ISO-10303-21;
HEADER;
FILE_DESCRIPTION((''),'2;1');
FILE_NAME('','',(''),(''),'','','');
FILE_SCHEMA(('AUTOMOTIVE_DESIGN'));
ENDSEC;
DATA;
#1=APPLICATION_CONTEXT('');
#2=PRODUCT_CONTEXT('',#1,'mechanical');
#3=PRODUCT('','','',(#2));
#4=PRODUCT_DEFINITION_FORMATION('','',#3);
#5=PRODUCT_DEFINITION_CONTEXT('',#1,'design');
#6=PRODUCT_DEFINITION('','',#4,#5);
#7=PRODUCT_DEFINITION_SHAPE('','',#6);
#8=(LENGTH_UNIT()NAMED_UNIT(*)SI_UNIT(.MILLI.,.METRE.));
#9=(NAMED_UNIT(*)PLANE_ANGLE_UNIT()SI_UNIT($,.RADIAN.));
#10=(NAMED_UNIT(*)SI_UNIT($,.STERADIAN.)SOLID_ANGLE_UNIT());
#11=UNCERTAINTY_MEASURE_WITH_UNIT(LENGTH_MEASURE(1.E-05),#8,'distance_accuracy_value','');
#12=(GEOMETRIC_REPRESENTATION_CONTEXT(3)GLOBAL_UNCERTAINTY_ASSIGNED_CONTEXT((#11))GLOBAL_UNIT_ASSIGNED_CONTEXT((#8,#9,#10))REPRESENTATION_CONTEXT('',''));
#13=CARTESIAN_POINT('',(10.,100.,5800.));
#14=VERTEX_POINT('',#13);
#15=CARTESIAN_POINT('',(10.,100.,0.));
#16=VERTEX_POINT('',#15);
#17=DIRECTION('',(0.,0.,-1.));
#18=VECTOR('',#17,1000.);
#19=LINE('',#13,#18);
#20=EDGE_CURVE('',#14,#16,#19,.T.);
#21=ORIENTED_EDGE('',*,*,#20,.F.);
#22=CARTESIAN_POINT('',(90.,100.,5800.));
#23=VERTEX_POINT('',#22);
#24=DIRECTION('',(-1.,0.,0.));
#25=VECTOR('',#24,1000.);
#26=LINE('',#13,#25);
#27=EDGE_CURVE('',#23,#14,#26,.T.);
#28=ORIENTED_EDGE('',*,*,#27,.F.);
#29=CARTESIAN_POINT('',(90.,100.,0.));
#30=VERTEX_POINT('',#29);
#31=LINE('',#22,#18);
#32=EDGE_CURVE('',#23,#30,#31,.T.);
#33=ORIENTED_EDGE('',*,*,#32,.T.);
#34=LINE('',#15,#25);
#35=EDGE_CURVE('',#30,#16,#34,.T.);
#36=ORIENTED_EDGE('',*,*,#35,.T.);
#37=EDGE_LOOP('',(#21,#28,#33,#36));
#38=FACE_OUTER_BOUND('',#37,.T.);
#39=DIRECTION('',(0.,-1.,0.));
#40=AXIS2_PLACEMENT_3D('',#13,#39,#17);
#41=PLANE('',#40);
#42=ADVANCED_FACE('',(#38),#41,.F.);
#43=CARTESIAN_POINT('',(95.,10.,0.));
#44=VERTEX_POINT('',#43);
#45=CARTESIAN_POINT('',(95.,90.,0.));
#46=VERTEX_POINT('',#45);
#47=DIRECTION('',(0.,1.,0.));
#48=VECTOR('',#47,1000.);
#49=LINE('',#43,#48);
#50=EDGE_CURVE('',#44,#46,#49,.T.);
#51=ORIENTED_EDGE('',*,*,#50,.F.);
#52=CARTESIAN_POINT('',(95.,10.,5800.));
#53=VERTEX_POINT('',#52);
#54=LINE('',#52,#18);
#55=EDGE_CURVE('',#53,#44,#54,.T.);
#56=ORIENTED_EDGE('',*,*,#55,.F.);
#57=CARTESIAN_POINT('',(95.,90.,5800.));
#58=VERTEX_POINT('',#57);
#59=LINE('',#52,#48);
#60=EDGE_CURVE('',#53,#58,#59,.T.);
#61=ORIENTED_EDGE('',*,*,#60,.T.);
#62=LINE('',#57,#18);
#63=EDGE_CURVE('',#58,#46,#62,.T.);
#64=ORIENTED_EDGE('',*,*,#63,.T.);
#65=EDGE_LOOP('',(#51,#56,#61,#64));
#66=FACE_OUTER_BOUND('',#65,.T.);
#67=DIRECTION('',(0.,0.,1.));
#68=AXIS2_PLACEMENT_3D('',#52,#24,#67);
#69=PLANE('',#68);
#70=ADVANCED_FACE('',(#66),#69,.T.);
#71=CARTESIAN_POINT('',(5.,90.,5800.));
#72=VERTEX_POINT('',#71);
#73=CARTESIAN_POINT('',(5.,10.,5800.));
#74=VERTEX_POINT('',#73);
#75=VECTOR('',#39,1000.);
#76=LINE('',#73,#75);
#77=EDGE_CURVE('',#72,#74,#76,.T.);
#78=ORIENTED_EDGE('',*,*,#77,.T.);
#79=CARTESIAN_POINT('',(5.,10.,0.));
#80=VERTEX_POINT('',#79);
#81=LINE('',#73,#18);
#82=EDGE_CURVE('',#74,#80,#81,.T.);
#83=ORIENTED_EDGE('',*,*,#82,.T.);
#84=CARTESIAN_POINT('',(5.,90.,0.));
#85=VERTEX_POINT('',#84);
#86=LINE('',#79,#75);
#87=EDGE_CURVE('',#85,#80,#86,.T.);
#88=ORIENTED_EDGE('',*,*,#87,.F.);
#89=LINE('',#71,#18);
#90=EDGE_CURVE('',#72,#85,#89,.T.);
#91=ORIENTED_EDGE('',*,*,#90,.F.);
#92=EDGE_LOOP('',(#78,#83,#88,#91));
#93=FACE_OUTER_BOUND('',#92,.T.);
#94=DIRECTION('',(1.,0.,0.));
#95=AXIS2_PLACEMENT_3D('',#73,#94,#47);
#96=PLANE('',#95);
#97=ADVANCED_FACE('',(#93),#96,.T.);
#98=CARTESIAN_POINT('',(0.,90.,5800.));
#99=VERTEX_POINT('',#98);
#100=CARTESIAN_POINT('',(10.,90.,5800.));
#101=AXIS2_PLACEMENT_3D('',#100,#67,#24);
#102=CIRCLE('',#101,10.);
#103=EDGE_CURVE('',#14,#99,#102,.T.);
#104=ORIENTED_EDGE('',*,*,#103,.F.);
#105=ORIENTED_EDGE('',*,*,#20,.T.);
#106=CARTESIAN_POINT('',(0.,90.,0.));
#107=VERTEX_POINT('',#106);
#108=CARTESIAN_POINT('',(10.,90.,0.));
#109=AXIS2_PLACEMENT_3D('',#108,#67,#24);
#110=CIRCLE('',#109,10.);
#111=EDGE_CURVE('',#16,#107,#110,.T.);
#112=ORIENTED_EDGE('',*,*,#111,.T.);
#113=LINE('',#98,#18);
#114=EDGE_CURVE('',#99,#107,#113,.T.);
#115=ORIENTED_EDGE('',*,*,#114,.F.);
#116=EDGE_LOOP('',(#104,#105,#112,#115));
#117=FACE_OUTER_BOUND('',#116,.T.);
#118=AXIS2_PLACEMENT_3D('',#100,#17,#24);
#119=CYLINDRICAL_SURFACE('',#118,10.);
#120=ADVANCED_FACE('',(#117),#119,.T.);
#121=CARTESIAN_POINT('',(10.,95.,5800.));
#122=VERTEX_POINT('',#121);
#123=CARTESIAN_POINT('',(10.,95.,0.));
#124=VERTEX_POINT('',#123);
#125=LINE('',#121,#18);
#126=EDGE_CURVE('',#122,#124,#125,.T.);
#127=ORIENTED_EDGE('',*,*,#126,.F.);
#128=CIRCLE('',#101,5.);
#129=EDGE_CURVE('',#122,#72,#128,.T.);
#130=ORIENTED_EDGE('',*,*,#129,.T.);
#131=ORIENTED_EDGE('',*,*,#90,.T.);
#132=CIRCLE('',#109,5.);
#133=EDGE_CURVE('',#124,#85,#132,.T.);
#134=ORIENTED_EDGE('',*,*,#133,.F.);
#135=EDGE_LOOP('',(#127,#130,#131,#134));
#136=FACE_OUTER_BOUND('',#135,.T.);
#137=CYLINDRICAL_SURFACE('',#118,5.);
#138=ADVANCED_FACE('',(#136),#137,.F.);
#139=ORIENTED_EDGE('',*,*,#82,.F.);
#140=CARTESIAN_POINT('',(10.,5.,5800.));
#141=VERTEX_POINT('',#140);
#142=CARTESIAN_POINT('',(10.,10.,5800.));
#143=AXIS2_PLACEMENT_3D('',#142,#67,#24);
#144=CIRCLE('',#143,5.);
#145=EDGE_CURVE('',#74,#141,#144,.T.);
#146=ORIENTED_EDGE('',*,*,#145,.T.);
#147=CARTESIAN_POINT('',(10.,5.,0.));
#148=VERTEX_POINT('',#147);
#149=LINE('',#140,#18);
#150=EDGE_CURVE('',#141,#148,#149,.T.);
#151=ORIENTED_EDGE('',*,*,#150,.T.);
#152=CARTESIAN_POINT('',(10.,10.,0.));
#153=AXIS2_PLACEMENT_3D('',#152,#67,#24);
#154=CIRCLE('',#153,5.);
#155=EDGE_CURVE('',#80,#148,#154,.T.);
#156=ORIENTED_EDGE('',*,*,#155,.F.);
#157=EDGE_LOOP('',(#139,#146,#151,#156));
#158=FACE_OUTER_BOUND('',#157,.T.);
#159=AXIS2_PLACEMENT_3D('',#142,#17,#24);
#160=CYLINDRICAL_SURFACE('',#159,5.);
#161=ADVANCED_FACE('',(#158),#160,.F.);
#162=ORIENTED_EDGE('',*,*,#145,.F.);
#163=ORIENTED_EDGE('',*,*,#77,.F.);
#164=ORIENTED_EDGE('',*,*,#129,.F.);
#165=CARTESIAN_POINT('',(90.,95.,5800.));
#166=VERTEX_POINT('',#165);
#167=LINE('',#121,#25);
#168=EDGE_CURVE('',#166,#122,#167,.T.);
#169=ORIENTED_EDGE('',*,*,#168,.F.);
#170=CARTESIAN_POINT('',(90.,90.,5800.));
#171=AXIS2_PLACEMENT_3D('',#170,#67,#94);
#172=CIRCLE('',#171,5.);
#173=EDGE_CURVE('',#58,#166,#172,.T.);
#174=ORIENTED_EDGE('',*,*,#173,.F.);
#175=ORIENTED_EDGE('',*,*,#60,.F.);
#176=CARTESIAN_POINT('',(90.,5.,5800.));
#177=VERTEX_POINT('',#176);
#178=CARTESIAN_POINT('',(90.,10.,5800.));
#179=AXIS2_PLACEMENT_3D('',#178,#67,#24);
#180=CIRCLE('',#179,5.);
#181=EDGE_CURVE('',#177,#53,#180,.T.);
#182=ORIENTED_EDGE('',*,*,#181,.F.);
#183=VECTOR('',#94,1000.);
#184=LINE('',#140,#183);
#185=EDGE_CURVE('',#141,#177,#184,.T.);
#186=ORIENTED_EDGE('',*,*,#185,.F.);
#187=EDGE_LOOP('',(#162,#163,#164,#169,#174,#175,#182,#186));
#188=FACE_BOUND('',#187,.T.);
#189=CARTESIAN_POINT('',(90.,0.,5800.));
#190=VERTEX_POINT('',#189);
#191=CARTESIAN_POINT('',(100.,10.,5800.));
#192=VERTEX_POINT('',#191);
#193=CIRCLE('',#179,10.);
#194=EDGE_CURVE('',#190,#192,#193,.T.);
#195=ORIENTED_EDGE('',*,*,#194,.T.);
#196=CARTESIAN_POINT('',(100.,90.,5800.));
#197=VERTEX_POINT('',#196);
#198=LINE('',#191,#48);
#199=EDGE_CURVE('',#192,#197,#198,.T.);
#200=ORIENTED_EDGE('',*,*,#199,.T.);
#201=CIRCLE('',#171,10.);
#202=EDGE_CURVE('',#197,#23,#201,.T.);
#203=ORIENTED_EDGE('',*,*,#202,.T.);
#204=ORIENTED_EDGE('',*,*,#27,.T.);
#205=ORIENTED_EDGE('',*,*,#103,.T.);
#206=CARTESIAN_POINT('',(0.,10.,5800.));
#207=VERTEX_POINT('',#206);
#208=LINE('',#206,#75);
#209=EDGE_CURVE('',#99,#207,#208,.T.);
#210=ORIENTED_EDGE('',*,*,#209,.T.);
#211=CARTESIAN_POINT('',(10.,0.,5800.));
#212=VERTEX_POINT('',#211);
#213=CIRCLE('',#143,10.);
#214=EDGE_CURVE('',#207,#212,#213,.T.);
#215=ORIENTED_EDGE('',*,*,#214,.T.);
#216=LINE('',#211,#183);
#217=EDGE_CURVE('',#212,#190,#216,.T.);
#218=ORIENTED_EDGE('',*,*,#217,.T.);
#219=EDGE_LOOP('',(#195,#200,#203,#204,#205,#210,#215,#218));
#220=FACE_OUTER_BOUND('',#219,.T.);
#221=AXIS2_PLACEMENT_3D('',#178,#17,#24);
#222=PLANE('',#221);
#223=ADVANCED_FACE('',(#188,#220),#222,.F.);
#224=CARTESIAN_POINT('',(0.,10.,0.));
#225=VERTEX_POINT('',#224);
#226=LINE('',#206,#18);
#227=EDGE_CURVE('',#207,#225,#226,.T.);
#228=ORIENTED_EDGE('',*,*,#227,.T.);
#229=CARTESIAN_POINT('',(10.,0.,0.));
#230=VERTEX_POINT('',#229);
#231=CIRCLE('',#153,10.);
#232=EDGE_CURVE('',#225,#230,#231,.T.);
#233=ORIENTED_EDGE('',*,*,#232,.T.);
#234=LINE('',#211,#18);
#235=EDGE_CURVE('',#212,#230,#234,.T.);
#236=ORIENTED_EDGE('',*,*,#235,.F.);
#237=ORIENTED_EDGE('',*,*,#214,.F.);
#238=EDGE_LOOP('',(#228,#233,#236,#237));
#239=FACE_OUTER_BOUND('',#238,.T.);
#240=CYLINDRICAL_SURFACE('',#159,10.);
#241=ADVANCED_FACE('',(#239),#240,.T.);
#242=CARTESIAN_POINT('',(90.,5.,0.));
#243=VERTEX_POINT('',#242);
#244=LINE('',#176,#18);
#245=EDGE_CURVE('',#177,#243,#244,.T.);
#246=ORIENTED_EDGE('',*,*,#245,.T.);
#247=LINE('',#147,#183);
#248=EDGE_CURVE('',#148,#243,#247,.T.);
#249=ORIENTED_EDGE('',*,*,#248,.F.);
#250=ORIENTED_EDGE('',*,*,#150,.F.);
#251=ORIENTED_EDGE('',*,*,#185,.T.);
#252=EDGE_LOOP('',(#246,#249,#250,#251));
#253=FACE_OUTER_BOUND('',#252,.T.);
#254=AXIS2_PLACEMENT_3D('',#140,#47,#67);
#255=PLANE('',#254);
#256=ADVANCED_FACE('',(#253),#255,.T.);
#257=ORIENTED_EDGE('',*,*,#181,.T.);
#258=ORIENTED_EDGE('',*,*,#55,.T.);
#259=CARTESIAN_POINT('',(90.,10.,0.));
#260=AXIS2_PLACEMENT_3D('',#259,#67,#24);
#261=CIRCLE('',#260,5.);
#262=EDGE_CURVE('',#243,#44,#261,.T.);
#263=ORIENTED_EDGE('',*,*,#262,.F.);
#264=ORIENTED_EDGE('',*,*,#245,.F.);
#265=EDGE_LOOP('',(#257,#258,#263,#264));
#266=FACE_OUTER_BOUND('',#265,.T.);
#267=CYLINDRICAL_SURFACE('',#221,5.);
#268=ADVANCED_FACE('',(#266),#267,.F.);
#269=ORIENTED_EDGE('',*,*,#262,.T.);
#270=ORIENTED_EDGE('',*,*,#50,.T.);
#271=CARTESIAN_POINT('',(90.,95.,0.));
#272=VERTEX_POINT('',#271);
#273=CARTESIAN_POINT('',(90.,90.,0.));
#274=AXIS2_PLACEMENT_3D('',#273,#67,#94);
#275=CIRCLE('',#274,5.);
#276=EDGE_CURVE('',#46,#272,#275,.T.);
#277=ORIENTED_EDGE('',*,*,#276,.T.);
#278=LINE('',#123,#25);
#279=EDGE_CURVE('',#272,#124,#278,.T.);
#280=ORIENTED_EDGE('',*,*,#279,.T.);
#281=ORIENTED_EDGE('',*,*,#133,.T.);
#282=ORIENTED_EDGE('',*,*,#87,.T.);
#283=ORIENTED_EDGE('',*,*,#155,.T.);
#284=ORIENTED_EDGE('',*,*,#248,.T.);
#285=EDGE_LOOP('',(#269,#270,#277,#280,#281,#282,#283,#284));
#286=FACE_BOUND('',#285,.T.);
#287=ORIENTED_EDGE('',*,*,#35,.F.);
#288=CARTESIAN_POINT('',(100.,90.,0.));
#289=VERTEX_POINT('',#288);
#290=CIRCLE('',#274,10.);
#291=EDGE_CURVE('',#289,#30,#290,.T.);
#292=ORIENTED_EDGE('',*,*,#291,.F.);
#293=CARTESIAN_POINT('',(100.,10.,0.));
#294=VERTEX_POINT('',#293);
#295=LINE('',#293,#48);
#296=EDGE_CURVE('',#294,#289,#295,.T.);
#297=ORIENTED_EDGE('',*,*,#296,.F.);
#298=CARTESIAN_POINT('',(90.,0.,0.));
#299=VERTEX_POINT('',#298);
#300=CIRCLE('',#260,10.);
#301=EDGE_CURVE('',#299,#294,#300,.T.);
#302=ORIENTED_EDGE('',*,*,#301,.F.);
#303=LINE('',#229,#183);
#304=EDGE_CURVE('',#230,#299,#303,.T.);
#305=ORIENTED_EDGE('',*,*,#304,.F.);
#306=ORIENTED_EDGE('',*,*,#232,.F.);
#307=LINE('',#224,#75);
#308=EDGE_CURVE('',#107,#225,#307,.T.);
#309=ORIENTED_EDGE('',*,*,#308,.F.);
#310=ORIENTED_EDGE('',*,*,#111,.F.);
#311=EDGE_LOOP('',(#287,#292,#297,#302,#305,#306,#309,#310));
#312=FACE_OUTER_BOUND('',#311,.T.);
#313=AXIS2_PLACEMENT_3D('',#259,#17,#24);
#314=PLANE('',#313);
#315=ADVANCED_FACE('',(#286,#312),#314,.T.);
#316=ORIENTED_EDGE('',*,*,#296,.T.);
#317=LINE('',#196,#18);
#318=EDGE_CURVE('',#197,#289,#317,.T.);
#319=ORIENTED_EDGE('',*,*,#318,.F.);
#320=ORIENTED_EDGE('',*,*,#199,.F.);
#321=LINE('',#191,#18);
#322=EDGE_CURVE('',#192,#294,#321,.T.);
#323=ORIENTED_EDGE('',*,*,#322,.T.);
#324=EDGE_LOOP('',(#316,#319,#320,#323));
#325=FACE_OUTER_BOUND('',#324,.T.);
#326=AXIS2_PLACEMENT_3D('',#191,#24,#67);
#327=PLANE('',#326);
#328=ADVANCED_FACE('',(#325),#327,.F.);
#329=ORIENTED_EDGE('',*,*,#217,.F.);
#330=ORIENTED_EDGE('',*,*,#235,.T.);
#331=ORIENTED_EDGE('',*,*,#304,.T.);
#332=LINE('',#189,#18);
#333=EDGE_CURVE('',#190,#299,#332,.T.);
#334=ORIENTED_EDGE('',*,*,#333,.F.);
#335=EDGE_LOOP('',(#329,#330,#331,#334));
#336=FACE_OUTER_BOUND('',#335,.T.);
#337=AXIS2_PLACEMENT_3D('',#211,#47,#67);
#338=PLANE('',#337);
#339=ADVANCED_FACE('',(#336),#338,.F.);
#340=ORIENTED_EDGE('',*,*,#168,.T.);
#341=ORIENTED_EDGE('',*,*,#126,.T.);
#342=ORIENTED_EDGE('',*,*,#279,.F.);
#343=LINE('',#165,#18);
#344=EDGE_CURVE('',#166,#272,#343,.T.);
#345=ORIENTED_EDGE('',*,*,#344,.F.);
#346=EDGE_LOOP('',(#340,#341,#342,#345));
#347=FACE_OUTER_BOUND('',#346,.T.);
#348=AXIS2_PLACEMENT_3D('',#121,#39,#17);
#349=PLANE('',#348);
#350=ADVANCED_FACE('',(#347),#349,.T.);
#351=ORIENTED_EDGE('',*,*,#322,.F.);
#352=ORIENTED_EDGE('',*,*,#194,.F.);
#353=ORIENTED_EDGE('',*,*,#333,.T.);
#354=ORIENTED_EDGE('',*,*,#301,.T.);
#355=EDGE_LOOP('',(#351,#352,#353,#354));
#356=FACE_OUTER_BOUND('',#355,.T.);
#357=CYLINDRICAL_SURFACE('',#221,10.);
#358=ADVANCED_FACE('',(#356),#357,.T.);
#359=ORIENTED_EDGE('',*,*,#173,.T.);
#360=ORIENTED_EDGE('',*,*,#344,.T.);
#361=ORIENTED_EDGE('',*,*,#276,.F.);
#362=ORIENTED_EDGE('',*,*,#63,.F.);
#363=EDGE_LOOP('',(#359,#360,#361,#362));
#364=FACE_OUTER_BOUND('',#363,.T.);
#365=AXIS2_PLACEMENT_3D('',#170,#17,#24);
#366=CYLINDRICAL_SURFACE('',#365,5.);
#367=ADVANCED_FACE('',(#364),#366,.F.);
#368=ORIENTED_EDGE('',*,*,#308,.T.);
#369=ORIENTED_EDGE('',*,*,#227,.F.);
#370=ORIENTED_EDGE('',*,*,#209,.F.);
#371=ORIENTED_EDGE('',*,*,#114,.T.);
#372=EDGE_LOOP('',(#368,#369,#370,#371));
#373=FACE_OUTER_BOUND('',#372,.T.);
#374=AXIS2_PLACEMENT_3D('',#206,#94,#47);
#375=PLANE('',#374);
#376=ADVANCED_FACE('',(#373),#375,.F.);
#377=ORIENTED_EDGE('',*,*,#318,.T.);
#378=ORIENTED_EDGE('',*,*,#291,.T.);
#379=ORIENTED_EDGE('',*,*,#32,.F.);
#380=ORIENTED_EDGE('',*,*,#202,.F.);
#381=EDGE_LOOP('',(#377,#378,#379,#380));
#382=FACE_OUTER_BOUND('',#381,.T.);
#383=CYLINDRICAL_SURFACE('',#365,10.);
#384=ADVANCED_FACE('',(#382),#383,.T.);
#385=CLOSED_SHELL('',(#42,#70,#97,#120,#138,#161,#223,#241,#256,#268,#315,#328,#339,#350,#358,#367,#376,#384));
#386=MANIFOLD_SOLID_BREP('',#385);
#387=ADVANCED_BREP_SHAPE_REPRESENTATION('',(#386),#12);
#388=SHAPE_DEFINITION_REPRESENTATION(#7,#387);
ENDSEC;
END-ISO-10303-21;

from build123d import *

# Parameters (mm, degrees)
BOSS_EXTRUDE1_DEPTH = 5800


with BuildPart() as part:
    # Sketch1 → Boss-Extrude1 (new body)
    with BuildSketch(Plane.XY):
        with BuildLine():
            Line((10, 0), (90, 0))
            ThreePointArc((90, 0), (97.071067812, 2.928932188), (100, 10))
            Line((100, 10), (100, 90))
            ThreePointArc((100, 90), (97.071067812, 97.071067812), (90, 100))
            Line((90, 100), (10, 100))
            ThreePointArc((10, 100), (2.928932188, 97.071067812), (0, 90))
            Line((0, 90), (0, 10))
            ThreePointArc((0, 10), (2.928932188, 2.928932188), (10, 0))
        make_face()
        with BuildLine():
            Line((10, 95), (90, 95))
            ThreePointArc((90, 95), (93.535533906, 93.535533906), (95, 90))
            Line((95, 90), (95, 10))
            ThreePointArc((95, 10), (93.535533906, 6.464466094), (90, 5))
            Line((90, 5), (10, 5))
            ThreePointArc((10, 5), (6.464466094, 6.464466094), (5, 10))
            Line((5, 10), (5, 90))
            ThreePointArc((5, 90), (6.464466094, 93.535533906), (10, 95))
        make_face(mode=Mode.SUBTRACT)
    extrude(amount=BOSS_EXTRUDE1_DEPTH)


solid = part.part
